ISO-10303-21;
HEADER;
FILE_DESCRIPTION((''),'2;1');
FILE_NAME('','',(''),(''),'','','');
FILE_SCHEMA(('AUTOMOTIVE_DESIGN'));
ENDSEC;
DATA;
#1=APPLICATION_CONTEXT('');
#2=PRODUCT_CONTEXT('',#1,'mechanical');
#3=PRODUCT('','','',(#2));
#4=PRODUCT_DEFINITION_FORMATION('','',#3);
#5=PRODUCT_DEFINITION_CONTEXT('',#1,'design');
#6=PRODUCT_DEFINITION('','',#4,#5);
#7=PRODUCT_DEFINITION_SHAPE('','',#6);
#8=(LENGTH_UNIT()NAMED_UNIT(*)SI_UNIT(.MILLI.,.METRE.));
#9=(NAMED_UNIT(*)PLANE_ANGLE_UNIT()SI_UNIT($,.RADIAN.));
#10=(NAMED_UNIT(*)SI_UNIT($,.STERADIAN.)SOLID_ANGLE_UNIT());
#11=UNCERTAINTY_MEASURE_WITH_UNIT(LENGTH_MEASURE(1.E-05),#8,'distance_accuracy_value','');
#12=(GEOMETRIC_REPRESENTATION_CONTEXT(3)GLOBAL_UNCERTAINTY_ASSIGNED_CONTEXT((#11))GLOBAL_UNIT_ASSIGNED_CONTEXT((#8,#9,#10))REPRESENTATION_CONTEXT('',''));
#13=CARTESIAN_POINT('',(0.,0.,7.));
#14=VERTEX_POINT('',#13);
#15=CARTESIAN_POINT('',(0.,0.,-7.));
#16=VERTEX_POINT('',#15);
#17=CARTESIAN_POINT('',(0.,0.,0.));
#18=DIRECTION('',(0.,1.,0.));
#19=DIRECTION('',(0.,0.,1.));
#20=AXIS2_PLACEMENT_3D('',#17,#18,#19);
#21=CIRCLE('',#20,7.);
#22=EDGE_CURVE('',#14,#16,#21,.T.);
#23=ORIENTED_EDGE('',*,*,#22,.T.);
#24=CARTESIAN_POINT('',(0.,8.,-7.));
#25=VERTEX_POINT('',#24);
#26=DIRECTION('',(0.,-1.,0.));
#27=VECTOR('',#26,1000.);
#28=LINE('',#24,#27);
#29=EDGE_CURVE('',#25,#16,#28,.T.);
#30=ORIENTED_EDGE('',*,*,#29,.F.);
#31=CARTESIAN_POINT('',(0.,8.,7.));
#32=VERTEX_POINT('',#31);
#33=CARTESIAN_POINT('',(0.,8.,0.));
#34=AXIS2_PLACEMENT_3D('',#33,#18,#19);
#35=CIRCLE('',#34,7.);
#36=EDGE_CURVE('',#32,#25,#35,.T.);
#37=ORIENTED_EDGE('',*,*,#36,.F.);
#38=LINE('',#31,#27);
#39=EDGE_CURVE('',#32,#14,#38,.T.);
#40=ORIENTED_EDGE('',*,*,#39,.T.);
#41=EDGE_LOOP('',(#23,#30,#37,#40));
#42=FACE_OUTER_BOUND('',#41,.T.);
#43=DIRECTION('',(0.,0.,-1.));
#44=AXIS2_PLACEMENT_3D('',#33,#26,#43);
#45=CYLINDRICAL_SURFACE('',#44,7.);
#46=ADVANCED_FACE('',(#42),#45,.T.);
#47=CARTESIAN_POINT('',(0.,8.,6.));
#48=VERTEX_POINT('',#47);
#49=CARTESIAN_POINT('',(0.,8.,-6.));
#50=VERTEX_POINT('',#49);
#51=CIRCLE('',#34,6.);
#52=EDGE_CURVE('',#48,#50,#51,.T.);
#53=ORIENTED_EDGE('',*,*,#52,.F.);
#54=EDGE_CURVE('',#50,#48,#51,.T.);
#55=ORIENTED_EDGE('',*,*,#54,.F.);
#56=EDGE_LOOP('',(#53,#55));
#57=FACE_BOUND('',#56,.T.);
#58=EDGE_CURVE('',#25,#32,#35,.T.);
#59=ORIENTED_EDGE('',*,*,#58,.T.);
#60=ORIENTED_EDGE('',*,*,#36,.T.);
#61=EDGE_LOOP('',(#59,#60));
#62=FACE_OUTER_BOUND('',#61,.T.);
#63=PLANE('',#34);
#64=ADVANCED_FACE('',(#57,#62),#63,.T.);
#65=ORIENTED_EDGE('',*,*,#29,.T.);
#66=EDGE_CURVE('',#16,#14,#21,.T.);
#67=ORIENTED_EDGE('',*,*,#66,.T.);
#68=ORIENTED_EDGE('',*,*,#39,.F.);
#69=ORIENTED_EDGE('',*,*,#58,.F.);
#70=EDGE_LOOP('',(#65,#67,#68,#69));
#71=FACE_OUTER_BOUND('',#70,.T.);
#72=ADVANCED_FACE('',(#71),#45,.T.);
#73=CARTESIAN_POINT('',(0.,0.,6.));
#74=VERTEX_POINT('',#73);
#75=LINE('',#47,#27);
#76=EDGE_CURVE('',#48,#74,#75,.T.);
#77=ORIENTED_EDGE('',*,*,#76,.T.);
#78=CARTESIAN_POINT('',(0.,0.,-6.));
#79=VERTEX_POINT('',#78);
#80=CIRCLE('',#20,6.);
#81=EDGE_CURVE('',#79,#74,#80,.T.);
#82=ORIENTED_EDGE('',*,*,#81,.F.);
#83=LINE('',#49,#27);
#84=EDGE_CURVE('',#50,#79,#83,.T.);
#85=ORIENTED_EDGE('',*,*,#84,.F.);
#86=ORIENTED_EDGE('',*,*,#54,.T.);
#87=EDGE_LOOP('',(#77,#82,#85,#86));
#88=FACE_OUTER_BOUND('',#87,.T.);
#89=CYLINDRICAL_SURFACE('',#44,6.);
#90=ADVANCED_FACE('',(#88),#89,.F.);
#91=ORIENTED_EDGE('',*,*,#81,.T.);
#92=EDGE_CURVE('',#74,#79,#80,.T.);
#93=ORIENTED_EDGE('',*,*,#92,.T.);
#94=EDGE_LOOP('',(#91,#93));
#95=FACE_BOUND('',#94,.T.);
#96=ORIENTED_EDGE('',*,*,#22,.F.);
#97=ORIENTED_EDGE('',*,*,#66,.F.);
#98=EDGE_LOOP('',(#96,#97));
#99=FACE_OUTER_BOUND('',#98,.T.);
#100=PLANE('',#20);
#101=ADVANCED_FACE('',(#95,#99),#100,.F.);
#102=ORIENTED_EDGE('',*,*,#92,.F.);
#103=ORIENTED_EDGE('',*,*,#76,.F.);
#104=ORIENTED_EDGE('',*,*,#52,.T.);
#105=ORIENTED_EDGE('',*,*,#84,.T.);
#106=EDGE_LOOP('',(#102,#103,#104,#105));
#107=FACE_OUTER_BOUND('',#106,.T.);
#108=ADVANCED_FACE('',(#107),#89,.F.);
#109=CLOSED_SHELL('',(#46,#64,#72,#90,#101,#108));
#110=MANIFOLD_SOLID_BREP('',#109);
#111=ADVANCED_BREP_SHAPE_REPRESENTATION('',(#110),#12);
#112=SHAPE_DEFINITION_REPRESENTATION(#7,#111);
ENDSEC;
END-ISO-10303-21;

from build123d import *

# Parameters (mm, degrees)
SKETCH1_R           = 7
SKETCH1_R_2         = 6
BOSS_EXTRUDE1_DEPTH = 8


with BuildPart() as part:
    # Sketch1 → Boss-Extrude1 (new body)
    with BuildSketch(Plane(origin=(0, 0, 0), x_dir=(1, 0, 0), z_dir=(0, 1, 0))):
        with Locations(Location((0, 0, 0), (0, 0, 270))):
            Circle(SKETCH1_R)
        with Locations(Location((0, 0, 0), (0, 0, 270))):
            Circle(SKETCH1_R_2, mode=Mode.SUBTRACT)
    extrude(amount=BOSS_EXTRUDE1_DEPTH)


solid = part.part
